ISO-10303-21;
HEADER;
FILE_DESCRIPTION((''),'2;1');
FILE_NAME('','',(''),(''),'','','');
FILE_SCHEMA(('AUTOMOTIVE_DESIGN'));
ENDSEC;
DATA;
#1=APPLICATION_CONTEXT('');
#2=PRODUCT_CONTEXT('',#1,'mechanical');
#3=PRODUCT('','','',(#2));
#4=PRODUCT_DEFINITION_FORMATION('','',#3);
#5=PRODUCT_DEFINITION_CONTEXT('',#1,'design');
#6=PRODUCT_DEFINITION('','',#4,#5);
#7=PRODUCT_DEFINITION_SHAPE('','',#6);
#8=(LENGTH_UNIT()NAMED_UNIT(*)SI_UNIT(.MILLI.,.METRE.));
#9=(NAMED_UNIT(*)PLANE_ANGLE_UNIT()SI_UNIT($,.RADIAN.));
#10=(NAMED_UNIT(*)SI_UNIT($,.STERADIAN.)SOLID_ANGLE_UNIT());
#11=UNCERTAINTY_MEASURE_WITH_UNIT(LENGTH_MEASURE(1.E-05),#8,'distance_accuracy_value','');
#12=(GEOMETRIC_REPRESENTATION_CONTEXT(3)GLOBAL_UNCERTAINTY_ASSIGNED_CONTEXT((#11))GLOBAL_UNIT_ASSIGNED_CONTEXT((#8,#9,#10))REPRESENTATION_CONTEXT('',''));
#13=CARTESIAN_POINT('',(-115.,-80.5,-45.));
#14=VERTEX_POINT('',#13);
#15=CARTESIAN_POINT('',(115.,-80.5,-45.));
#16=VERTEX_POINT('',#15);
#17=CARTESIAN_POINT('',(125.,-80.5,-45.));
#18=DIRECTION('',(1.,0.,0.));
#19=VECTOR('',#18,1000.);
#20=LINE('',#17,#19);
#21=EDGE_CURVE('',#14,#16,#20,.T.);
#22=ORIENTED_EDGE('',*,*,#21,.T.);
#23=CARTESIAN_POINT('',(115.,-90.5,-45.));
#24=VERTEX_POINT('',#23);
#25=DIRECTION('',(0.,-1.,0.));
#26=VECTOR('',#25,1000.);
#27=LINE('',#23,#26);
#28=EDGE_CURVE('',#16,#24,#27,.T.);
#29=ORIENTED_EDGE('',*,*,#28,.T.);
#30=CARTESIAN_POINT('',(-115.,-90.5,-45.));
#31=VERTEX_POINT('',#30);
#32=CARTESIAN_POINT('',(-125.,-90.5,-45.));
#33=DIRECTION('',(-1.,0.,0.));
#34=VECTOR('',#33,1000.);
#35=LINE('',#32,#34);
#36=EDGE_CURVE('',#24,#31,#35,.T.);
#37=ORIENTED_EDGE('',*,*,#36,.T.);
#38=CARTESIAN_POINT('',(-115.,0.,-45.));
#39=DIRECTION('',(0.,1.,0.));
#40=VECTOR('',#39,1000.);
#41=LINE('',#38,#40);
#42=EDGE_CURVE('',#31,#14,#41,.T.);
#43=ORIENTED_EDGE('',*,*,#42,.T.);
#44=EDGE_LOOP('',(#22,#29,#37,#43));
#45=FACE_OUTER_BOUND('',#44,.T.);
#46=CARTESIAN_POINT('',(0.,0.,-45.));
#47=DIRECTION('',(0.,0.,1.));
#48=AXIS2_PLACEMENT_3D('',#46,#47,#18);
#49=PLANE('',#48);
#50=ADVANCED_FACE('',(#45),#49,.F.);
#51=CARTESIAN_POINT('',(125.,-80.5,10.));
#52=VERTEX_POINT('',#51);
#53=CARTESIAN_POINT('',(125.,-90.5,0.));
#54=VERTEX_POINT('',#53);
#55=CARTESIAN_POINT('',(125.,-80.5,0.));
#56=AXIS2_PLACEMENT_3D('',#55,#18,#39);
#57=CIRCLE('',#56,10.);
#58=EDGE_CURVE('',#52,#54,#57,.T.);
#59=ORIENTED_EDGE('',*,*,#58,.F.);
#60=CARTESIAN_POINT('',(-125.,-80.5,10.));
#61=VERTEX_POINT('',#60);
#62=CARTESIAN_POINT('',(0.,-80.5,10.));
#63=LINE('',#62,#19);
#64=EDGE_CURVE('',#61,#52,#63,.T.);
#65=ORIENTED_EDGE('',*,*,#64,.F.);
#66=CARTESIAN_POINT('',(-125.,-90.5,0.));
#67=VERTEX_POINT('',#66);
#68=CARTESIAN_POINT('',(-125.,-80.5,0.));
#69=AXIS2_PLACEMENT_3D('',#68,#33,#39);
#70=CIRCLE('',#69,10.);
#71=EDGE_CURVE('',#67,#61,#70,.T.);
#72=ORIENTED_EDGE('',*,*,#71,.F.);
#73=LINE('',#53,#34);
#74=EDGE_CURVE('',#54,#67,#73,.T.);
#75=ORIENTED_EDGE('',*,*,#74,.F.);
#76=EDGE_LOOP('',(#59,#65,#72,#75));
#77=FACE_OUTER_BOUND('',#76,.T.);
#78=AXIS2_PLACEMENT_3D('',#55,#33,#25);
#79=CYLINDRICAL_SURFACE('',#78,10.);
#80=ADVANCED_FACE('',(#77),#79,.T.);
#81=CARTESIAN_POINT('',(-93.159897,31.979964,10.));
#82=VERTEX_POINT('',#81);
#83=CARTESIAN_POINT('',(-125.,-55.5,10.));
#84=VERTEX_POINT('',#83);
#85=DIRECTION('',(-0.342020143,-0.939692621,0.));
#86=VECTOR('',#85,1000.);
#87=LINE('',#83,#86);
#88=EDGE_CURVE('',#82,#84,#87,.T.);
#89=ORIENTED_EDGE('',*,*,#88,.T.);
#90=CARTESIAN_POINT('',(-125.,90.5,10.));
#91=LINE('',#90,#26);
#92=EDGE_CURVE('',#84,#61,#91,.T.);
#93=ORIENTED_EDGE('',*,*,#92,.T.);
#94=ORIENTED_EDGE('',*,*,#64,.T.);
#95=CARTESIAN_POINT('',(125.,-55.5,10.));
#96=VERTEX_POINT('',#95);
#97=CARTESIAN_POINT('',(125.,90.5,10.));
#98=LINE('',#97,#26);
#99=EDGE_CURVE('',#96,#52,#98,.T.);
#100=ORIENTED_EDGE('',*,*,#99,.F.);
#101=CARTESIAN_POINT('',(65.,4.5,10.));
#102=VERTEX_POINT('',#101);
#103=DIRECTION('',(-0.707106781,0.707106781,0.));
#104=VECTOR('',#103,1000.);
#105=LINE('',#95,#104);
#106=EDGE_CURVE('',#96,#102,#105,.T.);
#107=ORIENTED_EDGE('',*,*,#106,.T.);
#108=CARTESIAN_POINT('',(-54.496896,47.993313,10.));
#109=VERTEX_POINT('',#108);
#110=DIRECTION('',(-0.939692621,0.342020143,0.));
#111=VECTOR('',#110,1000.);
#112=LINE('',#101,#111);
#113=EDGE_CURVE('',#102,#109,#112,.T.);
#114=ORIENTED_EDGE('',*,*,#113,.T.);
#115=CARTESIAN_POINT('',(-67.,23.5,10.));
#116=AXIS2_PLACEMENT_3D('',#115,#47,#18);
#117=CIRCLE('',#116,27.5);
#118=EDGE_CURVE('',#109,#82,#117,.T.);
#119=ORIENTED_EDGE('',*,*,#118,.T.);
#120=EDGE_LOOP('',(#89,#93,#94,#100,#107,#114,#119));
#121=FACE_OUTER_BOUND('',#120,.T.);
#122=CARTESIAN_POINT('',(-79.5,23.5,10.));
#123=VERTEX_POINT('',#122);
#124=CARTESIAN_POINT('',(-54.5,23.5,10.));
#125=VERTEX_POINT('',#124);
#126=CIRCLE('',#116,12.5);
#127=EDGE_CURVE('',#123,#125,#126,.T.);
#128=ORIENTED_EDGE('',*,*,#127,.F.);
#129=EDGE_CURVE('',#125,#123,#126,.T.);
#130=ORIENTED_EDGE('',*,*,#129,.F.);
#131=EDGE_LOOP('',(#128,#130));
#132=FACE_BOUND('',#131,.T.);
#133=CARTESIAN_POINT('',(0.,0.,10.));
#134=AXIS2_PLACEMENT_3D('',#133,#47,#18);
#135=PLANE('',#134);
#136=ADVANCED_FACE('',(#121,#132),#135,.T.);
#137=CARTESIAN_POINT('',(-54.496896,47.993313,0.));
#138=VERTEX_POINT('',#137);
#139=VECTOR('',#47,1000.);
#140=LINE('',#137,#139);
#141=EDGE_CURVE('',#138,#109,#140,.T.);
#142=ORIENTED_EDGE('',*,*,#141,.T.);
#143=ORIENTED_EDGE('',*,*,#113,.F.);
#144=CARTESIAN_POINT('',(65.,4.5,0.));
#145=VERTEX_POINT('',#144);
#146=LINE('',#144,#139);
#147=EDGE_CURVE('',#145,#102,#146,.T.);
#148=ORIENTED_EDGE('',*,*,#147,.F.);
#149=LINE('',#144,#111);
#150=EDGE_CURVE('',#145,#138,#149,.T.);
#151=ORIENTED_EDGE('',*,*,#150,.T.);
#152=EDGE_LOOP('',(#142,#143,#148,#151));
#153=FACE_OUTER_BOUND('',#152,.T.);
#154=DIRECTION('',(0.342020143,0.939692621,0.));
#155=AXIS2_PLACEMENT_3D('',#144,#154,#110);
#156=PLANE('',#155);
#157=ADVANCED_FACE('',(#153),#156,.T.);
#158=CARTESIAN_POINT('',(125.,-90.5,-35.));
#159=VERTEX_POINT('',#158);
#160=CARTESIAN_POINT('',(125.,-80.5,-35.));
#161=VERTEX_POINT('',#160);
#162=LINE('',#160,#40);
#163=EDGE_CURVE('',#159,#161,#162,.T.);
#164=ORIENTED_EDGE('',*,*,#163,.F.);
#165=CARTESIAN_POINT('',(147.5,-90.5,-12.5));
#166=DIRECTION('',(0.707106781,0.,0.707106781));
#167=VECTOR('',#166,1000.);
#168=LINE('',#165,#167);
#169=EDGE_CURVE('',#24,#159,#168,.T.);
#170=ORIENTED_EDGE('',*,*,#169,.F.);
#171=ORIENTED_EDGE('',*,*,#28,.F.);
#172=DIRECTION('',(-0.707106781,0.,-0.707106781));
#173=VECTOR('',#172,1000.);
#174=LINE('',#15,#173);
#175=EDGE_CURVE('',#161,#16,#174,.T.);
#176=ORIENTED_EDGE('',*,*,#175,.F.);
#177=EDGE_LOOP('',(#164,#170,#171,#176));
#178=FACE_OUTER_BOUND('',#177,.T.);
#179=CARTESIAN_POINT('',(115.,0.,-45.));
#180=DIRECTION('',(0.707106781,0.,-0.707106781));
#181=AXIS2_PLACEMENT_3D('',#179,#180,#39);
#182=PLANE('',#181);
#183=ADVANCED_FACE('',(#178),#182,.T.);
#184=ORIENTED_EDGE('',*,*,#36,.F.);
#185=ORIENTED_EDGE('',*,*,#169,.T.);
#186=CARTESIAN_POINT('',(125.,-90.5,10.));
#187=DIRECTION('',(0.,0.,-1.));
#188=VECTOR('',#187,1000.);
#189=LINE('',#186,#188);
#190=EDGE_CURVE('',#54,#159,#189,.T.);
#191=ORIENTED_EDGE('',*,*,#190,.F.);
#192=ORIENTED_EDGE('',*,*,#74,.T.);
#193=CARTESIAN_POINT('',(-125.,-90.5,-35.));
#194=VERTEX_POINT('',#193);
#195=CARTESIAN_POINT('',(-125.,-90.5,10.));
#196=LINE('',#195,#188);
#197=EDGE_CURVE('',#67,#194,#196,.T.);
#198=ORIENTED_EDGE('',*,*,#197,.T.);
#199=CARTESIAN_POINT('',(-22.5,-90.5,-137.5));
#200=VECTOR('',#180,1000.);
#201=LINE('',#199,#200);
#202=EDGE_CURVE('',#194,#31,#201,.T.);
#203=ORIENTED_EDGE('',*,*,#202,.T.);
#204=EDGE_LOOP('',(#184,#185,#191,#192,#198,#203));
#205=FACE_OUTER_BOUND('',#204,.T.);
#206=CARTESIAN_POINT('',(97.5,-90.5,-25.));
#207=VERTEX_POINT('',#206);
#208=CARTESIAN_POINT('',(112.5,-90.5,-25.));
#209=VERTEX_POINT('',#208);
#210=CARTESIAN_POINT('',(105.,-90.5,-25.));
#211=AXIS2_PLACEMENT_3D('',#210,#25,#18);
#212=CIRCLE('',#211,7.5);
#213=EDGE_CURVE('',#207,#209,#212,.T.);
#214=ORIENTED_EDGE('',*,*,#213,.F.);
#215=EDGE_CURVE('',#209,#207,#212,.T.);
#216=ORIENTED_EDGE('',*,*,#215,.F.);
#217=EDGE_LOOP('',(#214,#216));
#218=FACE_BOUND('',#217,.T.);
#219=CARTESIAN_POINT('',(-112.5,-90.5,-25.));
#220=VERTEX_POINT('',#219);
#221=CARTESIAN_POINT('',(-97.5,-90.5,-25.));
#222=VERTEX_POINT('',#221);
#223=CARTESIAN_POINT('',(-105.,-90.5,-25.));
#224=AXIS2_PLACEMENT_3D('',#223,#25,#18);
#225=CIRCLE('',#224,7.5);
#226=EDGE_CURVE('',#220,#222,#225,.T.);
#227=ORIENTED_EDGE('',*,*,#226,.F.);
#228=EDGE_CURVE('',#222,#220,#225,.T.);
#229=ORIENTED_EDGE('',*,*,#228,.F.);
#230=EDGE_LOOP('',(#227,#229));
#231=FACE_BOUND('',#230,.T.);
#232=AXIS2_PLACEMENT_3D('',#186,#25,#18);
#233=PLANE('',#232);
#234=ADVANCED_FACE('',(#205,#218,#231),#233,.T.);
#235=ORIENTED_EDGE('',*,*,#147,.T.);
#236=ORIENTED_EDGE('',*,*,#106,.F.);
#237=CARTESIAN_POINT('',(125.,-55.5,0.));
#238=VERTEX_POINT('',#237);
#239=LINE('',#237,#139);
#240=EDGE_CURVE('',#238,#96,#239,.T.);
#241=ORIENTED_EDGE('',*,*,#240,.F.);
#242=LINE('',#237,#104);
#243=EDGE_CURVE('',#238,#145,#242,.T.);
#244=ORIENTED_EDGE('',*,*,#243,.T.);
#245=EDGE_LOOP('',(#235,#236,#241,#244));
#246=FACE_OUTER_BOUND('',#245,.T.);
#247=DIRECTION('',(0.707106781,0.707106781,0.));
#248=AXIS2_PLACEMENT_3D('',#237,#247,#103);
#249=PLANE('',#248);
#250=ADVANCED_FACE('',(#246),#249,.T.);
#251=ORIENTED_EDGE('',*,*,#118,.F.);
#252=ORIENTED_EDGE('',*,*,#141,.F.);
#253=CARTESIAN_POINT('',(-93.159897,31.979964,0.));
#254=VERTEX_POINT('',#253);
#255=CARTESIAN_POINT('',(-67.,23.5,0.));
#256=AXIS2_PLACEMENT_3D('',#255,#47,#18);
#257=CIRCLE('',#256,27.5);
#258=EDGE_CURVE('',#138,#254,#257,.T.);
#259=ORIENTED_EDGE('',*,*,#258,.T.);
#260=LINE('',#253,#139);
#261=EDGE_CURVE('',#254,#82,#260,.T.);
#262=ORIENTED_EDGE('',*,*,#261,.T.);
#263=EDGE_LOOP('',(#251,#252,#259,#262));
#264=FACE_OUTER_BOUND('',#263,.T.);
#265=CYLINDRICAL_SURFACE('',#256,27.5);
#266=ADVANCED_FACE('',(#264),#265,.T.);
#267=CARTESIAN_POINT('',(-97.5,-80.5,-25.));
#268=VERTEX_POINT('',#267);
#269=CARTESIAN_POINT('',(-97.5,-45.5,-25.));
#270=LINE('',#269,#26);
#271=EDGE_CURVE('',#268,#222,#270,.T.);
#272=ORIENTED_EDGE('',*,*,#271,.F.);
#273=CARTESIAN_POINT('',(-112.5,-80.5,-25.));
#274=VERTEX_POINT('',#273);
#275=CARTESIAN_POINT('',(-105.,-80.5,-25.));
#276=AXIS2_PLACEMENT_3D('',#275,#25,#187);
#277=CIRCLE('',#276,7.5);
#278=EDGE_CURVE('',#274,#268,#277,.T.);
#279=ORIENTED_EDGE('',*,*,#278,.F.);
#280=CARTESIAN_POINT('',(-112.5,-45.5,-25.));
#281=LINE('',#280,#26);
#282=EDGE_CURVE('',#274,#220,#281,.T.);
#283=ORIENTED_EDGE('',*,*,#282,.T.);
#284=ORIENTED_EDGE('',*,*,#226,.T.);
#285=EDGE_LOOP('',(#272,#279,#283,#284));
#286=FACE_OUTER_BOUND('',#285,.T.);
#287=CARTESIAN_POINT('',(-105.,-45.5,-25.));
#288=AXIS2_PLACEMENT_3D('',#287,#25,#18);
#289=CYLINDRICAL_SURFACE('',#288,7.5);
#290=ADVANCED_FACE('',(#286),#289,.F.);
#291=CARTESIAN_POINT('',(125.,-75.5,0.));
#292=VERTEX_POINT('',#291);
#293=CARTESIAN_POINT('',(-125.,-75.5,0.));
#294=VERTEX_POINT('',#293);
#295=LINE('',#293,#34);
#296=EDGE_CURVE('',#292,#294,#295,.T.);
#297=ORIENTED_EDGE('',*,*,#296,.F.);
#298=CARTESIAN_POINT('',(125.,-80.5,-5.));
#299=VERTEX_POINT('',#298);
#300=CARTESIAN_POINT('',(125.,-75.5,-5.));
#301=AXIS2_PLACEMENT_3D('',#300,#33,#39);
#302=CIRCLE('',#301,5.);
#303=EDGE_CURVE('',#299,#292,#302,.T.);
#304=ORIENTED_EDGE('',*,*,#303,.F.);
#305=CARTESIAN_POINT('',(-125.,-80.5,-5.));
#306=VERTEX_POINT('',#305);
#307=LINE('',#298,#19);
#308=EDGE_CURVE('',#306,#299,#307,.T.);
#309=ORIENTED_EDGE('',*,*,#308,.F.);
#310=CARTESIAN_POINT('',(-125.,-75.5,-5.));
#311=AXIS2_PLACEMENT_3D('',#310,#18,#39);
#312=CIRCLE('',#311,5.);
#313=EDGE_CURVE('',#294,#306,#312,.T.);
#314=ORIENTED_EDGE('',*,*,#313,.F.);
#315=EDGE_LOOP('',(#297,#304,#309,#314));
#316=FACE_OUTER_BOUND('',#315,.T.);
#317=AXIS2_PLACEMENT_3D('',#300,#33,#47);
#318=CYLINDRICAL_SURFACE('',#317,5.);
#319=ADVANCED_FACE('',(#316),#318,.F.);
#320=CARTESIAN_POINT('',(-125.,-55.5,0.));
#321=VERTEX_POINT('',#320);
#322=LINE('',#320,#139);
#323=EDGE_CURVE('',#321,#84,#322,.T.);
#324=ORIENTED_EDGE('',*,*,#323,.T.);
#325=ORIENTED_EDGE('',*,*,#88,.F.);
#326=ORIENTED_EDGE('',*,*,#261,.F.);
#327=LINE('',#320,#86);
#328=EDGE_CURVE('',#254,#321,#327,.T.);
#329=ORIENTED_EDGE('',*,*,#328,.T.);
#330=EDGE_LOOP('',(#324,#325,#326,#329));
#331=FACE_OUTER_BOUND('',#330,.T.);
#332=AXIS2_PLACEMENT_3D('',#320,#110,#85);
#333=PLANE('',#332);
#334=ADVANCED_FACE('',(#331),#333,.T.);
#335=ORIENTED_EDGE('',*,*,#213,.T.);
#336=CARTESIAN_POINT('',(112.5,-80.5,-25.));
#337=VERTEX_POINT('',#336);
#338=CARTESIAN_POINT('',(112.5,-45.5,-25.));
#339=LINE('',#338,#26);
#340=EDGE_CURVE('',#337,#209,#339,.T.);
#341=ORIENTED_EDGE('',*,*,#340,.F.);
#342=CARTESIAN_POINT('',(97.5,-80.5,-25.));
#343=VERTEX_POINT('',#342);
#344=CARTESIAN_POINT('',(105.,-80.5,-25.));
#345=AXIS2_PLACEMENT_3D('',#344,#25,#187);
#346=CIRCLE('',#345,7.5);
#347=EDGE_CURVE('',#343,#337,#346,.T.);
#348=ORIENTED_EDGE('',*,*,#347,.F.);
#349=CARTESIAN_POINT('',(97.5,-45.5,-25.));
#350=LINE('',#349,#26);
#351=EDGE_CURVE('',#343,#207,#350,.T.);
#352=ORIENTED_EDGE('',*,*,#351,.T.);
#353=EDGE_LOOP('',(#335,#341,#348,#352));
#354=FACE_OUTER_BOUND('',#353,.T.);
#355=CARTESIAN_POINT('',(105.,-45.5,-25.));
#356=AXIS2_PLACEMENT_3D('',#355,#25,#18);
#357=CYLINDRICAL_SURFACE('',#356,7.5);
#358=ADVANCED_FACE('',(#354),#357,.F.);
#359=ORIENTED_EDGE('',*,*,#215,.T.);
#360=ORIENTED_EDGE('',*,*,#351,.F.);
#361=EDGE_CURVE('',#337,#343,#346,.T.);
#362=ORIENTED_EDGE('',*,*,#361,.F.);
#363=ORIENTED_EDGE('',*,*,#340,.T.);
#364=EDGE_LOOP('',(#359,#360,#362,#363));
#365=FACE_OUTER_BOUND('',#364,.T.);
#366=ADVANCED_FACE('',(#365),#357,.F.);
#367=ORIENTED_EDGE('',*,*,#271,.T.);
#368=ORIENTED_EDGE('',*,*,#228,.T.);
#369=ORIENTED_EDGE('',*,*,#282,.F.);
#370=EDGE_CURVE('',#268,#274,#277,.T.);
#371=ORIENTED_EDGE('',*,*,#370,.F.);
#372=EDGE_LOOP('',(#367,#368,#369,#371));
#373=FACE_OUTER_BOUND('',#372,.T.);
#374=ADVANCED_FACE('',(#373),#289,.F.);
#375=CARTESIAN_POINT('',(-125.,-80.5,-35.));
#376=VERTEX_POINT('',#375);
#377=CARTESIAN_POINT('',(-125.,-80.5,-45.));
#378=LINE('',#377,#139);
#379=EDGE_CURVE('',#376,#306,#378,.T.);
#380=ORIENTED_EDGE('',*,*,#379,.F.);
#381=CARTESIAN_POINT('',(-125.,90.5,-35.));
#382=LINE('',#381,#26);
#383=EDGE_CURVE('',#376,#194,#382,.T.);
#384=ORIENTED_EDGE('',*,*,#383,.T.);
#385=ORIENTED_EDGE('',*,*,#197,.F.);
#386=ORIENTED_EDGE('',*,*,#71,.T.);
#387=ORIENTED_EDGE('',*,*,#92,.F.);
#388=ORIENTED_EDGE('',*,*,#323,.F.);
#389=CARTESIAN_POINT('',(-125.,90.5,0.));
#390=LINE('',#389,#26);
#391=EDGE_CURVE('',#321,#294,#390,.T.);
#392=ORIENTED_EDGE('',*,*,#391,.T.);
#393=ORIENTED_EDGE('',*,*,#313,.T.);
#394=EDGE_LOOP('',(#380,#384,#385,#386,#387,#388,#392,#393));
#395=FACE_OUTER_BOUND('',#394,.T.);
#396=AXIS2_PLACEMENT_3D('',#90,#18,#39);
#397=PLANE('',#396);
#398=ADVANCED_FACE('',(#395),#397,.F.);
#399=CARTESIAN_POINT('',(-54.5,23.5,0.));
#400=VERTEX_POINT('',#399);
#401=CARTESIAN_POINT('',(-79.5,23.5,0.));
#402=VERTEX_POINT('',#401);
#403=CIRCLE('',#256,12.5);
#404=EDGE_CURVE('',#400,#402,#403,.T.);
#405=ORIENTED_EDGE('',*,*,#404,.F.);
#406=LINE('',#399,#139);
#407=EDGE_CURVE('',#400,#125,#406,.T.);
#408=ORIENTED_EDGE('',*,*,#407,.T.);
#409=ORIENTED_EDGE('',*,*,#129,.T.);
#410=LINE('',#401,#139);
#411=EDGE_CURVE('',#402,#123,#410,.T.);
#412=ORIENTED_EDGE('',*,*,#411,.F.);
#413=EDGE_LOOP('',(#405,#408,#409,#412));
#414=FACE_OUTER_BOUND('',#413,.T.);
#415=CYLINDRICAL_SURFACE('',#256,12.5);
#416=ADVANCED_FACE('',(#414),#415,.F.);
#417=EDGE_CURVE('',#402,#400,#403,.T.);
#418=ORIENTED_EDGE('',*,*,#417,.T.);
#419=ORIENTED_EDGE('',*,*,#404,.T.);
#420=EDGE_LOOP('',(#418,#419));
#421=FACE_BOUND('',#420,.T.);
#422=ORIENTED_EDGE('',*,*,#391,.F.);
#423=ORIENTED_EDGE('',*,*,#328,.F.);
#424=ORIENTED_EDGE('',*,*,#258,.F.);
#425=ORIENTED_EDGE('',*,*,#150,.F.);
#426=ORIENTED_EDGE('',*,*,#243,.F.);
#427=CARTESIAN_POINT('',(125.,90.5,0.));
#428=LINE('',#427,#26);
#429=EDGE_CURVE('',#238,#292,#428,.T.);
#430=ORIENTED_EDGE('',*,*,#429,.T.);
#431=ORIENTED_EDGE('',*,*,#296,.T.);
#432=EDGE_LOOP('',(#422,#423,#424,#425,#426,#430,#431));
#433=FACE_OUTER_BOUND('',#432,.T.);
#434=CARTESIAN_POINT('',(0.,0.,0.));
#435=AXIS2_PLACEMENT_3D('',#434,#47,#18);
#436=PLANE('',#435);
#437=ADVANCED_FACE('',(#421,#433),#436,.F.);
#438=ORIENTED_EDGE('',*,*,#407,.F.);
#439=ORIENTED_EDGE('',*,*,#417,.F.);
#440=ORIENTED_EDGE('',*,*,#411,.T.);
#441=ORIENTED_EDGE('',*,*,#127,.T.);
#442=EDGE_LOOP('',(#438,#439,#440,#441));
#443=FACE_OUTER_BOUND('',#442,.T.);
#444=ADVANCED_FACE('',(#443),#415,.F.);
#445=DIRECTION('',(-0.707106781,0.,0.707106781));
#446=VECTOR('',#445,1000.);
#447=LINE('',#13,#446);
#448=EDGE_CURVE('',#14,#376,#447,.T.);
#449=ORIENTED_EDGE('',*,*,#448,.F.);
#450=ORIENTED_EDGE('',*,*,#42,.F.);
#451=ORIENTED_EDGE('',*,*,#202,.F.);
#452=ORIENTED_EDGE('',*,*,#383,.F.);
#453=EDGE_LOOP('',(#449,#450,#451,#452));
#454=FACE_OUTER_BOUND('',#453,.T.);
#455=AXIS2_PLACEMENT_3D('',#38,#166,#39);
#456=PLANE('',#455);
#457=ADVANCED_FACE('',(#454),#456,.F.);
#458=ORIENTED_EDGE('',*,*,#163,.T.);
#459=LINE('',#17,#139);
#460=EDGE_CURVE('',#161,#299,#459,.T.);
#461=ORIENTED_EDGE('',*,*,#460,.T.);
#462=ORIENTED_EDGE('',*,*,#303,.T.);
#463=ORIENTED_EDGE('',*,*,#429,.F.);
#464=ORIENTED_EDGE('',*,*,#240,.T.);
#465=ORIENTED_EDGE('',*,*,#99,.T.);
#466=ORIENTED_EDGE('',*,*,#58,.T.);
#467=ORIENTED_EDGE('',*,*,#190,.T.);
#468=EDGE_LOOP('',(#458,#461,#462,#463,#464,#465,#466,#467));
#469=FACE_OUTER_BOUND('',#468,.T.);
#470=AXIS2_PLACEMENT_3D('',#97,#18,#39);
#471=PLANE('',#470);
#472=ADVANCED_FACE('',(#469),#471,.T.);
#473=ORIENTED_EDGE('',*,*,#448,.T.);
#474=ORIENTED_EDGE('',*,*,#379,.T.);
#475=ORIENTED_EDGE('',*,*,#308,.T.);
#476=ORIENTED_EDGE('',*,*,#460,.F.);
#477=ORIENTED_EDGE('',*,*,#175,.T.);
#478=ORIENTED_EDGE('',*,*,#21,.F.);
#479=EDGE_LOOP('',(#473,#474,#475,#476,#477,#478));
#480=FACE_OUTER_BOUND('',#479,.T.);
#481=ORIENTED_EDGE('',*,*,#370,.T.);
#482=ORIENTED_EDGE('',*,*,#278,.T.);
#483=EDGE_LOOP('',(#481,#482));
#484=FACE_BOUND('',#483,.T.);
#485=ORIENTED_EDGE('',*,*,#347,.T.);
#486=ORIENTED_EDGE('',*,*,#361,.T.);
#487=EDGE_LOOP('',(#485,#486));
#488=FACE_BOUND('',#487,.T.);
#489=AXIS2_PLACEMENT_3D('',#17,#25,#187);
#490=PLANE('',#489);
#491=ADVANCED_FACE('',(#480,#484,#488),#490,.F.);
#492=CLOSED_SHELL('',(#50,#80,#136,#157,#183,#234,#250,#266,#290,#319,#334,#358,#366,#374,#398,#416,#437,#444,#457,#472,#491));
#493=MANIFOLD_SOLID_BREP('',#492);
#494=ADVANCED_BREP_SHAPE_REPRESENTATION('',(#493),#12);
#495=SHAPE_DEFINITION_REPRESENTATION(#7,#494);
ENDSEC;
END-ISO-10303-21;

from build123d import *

# Parameters (mm, degrees)
SKETCH1_W           = 250
SKETCH1_H           = 181
BOSS_EXTRUDE1_DEPTH = 10
SKETCH2_OUTSIDE_W   = 313.762
SKETCH2_OUTSIDE_H   = 244.762
CUT_EXTRUDE1_DEPTH  = 10
SKETCH3_R           = 12.5
CUT_EXTRUDE2_DEPTH  = 10
SKETCH4_W           = 250
SKETCH4_H           = 10
BOSS_EXTRUDE2_DEPTH = 45
FILLET1_R           = 10
FILLET2_R           = 5
SKETCH5_R           = 7.5
CUT_EXTRUDE3_DEPTH  = 45
CHAMFER1_SIZE       = 10


with BuildPart() as part:
    # Sketch1 → Boss-Extrude1 (new body)
    with BuildSketch(Plane.XY):
        Rectangle(SKETCH1_W, SKETCH1_H)
    extrude(amount=BOSS_EXTRUDE1_DEPTH)

    # Sketch2 outside → Cut-Extrude1 (cut)
    with BuildSketch(Plane.XY.offset(10)):
        Rectangle(SKETCH2_OUTSIDE_W, SKETCH2_OUTSIDE_H)
        with BuildLine():
            Line((-125, -55.5), (-93.159896838, 31.97996447))
            ThreePointArc((-93.159896838, 31.97996447), (-77.523014584, 48.907010136), (-54.496896373, 47.993313367))
            Line((-54.496896373, 47.993313367), (65, 4.5))
            Line((65, 4.5), (125, -55.5))
            Line((125, -55.5), (125, -90.5))
            Line((125, -90.5), (-125, -90.5))
            Line((-125, -90.5), (-125, -55.5))
        make_face(mode=Mode.SUBTRACT)
    extrude(amount=-CUT_EXTRUDE1_DEPTH, mode=Mode.SUBTRACT)

    # Sketch3 → Cut-Extrude2 (cut)
    with BuildSketch(Plane.XY.offset(10)):
        with Locations((-67, 23.5)):
            Circle(SKETCH3_R)
    extrude(amount=-CUT_EXTRUDE2_DEPTH, mode=Mode.SUBTRACT)

    # Sketch4 → Boss-Extrude2 (add)
    with BuildSketch(Plane(origin=(0, 0, 0), x_dir=(-1, 0, 0), z_dir=(0, 0, -1))):
        with Locations((0, -85.5)):
            Rectangle(SKETCH4_W, SKETCH4_H)
    extrude(amount=BOSS_EXTRUDE2_DEPTH)

    # Fillet1
    fillet1_edges = [part.edges().sort_by_distance(p)[0] for p in [
        (0, -90.5, 10),
    ]]
    fillet(fillet1_edges, radius=FILLET1_R)

    # Fillet2
    fillet2_edges = [part.edges().sort_by_distance(p)[0] for p in [
        (0, -80.5, 0),
    ]]
    fillet(fillet2_edges, radius=FILLET2_R)

    # Sketch5 → Cut-Extrude3 (cut)
    with BuildSketch(Plane.XZ.offset(90.5)):
        with Locations((-105, -25)):
            Circle(SKETCH5_R)
        with Locations((105, -25)):
            Circle(SKETCH5_R)
    extrude(amount=-CUT_EXTRUDE3_DEPTH, mode=Mode.SUBTRACT)

    # Chamfer1
    chamfer1_edges = [part.edges().sort_by_distance(p)[0] for p in [
        (125, -85.5, -45),
        (-125, -85.5, -45),
    ]]
    chamfer(chamfer1_edges, length=CHAMFER1_SIZE)


solid = part.part
